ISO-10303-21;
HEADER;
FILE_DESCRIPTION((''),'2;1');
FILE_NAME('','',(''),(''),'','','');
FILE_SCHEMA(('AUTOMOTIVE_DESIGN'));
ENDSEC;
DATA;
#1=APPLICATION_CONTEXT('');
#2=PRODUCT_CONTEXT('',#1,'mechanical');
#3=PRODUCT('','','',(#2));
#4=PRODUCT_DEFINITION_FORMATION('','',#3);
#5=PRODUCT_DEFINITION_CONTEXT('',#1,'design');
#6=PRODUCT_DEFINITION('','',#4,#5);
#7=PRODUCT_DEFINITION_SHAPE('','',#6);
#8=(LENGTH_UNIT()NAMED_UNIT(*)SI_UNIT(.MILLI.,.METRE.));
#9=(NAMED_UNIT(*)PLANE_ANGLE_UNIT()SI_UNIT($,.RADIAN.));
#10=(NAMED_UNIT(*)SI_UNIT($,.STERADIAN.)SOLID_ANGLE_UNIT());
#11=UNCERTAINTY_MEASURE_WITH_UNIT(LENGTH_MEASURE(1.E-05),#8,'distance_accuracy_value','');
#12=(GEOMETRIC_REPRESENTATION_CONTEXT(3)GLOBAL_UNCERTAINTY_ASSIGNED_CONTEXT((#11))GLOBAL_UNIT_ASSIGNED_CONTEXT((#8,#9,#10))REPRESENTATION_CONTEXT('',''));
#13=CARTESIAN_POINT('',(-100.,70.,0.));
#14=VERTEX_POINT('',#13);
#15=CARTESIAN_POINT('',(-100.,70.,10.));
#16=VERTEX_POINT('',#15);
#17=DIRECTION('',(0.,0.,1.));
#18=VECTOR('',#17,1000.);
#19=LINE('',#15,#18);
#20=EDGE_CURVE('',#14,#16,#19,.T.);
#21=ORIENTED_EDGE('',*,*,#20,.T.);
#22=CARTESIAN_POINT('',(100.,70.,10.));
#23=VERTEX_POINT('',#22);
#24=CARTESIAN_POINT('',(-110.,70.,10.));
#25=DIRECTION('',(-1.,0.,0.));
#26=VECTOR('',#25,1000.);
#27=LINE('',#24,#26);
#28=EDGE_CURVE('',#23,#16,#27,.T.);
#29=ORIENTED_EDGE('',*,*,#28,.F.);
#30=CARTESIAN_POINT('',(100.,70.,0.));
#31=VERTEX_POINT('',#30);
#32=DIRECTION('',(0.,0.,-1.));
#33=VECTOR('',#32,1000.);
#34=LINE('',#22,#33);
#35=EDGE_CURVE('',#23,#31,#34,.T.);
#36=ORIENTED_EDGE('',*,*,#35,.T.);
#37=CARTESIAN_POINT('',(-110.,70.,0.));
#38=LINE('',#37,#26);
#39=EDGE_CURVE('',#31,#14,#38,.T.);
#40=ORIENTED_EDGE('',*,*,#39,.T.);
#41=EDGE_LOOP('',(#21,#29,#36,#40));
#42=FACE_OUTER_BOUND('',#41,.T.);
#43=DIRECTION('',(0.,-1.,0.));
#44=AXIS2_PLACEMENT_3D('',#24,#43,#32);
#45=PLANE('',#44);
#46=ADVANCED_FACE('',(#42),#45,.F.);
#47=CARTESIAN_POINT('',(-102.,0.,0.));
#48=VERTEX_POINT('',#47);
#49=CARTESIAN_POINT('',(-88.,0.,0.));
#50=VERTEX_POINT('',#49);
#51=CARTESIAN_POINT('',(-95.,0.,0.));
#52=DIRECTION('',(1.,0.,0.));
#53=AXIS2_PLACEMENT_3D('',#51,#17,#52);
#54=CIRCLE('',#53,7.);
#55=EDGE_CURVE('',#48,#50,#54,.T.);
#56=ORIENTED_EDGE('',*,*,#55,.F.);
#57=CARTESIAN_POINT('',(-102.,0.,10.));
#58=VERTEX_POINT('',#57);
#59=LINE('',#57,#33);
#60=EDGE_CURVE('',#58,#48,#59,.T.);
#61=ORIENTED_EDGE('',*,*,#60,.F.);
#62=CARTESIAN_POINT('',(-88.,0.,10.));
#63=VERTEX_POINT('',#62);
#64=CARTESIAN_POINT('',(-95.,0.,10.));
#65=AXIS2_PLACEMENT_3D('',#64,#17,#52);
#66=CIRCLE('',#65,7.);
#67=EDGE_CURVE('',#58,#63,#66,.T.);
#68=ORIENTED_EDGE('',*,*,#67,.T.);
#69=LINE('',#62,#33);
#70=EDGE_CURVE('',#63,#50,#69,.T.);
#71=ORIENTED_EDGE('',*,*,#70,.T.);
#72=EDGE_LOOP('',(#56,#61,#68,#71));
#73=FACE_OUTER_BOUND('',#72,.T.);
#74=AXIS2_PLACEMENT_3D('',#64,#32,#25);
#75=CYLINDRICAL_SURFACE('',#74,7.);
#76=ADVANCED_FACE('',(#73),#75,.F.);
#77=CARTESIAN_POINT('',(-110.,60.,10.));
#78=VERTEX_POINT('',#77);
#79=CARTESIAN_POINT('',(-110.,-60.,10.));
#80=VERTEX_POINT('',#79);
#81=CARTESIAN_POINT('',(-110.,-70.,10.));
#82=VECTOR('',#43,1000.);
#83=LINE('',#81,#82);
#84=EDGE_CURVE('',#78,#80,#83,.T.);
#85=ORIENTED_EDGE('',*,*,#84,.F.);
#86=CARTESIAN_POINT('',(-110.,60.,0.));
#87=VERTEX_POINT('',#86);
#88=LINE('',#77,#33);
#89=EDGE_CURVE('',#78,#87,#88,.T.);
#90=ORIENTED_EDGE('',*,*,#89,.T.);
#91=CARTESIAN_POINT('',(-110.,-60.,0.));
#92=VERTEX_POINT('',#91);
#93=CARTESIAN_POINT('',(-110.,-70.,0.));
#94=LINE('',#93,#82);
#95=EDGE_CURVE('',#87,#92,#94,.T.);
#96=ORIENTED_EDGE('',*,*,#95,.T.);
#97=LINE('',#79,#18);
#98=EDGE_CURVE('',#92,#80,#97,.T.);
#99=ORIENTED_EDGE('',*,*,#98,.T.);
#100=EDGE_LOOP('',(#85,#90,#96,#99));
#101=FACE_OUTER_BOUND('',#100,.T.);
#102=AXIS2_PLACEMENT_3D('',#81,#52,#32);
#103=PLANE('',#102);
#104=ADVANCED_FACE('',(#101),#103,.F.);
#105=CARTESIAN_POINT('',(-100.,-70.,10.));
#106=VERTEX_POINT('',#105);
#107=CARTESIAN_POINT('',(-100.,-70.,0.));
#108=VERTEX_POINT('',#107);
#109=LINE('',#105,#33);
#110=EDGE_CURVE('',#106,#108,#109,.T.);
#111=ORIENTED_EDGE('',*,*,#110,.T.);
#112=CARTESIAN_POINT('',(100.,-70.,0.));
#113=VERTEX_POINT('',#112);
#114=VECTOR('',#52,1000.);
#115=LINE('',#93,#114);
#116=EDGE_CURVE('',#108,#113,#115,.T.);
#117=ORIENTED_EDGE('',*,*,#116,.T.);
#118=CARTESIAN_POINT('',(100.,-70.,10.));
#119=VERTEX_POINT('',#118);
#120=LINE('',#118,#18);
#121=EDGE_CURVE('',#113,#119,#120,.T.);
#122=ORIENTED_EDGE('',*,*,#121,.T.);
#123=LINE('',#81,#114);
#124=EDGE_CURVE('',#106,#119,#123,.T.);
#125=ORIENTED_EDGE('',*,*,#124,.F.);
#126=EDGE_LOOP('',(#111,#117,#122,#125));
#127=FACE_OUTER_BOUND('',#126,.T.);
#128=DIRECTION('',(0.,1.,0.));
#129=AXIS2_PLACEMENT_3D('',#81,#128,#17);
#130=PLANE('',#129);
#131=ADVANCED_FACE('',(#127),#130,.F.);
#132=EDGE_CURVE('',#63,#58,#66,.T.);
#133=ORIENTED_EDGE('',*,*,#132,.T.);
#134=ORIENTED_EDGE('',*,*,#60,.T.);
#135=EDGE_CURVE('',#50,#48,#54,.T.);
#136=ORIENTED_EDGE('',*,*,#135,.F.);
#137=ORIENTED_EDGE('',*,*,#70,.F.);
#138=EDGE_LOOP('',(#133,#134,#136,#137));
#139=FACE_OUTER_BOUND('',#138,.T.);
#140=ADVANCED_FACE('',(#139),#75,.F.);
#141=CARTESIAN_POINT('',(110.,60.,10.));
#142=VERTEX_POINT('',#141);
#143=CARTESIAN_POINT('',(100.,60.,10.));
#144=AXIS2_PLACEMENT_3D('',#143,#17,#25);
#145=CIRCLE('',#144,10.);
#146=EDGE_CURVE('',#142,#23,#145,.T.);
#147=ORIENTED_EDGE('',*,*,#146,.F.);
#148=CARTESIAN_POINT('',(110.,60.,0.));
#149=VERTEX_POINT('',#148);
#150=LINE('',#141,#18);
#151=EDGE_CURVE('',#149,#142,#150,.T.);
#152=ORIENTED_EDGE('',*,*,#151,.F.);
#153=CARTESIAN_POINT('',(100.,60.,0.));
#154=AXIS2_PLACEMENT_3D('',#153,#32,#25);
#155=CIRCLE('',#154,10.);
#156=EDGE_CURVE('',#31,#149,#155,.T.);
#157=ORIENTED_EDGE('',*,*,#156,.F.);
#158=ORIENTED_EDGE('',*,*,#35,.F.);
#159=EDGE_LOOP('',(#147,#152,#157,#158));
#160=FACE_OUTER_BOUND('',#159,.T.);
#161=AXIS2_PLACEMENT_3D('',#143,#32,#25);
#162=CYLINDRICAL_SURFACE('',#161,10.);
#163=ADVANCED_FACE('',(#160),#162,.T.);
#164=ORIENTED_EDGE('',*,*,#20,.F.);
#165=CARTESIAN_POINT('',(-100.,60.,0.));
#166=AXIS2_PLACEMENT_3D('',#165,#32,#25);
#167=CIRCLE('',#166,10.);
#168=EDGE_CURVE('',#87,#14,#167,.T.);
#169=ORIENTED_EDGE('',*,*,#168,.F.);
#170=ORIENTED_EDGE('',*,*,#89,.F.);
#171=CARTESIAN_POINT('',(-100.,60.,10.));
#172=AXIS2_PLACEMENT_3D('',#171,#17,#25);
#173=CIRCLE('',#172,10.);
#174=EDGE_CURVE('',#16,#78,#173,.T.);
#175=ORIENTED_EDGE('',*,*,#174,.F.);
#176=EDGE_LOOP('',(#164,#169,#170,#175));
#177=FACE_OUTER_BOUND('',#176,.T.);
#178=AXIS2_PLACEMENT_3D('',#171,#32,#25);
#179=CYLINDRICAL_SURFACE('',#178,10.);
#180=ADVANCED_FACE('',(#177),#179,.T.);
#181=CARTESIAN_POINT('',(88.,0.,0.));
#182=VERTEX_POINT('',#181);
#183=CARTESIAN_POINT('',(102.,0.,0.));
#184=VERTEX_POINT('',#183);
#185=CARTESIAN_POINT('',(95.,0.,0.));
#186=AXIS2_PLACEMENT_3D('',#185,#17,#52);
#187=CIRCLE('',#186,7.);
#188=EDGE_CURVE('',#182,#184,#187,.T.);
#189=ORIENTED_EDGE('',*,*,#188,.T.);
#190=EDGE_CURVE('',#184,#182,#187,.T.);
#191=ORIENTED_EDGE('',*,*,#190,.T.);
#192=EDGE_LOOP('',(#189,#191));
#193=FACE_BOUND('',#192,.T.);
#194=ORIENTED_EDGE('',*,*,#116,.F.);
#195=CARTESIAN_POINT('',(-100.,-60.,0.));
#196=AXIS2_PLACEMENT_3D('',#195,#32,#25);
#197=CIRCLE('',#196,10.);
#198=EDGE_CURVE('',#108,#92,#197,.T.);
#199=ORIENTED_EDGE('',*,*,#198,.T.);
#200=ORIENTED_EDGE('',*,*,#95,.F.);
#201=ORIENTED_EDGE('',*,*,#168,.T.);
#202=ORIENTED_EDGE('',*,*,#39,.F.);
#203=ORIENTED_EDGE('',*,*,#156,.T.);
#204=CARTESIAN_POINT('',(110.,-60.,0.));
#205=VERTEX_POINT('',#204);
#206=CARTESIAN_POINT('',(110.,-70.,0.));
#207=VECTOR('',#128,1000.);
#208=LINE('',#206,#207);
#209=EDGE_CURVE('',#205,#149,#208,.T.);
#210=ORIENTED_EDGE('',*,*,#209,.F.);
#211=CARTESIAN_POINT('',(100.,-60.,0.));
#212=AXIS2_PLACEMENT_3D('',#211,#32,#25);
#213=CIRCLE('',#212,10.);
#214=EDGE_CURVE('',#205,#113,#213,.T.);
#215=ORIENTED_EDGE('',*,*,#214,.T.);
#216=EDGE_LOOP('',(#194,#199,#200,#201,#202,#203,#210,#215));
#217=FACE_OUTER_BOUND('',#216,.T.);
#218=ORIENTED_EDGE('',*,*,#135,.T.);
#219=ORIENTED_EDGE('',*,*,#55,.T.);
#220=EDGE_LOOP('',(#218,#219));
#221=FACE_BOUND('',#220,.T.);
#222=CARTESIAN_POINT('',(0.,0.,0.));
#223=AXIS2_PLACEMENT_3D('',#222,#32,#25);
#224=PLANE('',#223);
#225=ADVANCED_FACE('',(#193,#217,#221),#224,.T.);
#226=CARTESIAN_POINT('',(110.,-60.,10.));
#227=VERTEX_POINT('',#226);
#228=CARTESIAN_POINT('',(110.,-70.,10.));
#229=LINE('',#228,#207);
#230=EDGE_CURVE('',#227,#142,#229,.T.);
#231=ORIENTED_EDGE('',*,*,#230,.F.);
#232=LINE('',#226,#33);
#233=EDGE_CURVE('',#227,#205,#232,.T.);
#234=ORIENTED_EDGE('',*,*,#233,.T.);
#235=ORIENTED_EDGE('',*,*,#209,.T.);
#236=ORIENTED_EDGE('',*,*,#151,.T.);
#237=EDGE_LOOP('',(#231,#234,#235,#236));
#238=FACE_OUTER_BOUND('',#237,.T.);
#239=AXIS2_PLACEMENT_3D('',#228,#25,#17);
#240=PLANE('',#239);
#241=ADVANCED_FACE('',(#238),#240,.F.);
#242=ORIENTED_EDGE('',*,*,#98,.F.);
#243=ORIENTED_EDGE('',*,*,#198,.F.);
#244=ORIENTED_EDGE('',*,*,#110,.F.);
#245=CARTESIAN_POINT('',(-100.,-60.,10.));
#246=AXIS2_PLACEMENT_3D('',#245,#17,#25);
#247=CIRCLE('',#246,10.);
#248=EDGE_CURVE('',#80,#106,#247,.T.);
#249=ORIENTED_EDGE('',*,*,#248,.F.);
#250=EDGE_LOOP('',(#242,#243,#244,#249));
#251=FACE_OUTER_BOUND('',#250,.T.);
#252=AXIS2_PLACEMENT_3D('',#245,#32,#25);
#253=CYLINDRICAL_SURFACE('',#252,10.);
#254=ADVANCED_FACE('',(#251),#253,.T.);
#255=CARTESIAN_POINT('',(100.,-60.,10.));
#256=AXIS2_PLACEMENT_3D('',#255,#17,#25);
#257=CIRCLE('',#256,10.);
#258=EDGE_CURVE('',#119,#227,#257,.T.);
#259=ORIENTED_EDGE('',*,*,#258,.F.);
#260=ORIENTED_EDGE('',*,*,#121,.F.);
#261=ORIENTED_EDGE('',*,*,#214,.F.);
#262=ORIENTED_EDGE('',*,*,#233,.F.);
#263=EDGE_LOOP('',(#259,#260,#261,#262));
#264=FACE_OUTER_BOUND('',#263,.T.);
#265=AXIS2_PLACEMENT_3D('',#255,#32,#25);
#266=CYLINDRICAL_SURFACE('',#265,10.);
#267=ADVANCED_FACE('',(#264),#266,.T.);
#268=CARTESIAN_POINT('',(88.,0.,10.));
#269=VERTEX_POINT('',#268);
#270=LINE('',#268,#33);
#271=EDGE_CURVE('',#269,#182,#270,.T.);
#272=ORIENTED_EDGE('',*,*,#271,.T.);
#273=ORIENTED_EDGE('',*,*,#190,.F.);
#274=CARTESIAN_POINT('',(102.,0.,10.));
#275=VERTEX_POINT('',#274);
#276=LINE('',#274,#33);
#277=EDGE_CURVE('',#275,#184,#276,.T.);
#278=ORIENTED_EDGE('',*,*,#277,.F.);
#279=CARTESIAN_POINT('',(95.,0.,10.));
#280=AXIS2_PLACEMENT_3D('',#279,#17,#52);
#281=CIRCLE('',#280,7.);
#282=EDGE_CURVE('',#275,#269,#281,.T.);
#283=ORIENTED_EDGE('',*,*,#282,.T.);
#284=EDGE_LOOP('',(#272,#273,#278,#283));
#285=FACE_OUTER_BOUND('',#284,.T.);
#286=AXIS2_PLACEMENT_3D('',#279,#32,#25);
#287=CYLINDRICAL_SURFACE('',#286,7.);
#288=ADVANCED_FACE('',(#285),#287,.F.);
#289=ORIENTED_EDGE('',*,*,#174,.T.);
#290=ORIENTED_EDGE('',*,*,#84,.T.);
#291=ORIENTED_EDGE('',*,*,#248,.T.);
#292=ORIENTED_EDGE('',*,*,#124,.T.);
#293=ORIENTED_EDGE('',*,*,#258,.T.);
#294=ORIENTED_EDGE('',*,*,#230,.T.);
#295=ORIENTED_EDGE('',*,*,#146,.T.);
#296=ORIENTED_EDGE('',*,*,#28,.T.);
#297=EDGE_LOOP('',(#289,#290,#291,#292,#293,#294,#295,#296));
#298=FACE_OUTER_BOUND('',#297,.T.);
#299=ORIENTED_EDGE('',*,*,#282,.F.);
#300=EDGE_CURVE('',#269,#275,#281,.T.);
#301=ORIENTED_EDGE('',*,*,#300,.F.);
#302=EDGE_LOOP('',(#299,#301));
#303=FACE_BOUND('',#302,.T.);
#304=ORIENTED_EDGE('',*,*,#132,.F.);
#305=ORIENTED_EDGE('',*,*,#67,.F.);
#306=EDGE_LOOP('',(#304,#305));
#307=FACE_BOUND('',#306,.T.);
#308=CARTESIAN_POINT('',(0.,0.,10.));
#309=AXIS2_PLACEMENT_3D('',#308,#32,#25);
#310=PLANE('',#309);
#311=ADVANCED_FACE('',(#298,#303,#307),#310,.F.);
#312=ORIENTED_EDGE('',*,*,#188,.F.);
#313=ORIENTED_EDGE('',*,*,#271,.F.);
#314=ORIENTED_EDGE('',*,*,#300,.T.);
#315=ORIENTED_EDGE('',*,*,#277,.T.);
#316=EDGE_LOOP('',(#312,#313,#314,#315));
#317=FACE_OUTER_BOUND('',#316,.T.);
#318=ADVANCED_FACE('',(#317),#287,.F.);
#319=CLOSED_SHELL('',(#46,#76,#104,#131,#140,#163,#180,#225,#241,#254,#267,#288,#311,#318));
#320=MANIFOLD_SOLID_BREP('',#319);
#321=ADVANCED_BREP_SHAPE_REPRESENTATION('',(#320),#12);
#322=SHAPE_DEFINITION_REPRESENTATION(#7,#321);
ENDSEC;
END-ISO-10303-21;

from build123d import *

# Parameters (mm, degrees)
SKETCH1_W           = 220
SKETCH1_H           = 140
SKETCH1_R           = 7
BOSS_EXTRUDE1_DEPTH = 10
FILLET1_R           = 10


with BuildPart() as part:
    # Sketch1 → Boss-Extrude1 (new body)
    with BuildSketch(Plane.XY):
        Rectangle(SKETCH1_W, SKETCH1_H)
        with Locations((-95, 0)):
            Circle(SKETCH1_R, mode=Mode.SUBTRACT)
        with Locations((95, 0)):
            Circle(SKETCH1_R, mode=Mode.SUBTRACT)
    extrude(amount=BOSS_EXTRUDE1_DEPTH)

    # Fillet1
    fillet1_edges = [part.edges().sort_by_distance(p)[0] for p in [
        (-110, 70, 5),
        (110, 70, 5),
        (110, -70, 5),
        (-110, -70, 5),
    ]]
    fillet(fillet1_edges, radius=FILLET1_R)


solid = part.part
